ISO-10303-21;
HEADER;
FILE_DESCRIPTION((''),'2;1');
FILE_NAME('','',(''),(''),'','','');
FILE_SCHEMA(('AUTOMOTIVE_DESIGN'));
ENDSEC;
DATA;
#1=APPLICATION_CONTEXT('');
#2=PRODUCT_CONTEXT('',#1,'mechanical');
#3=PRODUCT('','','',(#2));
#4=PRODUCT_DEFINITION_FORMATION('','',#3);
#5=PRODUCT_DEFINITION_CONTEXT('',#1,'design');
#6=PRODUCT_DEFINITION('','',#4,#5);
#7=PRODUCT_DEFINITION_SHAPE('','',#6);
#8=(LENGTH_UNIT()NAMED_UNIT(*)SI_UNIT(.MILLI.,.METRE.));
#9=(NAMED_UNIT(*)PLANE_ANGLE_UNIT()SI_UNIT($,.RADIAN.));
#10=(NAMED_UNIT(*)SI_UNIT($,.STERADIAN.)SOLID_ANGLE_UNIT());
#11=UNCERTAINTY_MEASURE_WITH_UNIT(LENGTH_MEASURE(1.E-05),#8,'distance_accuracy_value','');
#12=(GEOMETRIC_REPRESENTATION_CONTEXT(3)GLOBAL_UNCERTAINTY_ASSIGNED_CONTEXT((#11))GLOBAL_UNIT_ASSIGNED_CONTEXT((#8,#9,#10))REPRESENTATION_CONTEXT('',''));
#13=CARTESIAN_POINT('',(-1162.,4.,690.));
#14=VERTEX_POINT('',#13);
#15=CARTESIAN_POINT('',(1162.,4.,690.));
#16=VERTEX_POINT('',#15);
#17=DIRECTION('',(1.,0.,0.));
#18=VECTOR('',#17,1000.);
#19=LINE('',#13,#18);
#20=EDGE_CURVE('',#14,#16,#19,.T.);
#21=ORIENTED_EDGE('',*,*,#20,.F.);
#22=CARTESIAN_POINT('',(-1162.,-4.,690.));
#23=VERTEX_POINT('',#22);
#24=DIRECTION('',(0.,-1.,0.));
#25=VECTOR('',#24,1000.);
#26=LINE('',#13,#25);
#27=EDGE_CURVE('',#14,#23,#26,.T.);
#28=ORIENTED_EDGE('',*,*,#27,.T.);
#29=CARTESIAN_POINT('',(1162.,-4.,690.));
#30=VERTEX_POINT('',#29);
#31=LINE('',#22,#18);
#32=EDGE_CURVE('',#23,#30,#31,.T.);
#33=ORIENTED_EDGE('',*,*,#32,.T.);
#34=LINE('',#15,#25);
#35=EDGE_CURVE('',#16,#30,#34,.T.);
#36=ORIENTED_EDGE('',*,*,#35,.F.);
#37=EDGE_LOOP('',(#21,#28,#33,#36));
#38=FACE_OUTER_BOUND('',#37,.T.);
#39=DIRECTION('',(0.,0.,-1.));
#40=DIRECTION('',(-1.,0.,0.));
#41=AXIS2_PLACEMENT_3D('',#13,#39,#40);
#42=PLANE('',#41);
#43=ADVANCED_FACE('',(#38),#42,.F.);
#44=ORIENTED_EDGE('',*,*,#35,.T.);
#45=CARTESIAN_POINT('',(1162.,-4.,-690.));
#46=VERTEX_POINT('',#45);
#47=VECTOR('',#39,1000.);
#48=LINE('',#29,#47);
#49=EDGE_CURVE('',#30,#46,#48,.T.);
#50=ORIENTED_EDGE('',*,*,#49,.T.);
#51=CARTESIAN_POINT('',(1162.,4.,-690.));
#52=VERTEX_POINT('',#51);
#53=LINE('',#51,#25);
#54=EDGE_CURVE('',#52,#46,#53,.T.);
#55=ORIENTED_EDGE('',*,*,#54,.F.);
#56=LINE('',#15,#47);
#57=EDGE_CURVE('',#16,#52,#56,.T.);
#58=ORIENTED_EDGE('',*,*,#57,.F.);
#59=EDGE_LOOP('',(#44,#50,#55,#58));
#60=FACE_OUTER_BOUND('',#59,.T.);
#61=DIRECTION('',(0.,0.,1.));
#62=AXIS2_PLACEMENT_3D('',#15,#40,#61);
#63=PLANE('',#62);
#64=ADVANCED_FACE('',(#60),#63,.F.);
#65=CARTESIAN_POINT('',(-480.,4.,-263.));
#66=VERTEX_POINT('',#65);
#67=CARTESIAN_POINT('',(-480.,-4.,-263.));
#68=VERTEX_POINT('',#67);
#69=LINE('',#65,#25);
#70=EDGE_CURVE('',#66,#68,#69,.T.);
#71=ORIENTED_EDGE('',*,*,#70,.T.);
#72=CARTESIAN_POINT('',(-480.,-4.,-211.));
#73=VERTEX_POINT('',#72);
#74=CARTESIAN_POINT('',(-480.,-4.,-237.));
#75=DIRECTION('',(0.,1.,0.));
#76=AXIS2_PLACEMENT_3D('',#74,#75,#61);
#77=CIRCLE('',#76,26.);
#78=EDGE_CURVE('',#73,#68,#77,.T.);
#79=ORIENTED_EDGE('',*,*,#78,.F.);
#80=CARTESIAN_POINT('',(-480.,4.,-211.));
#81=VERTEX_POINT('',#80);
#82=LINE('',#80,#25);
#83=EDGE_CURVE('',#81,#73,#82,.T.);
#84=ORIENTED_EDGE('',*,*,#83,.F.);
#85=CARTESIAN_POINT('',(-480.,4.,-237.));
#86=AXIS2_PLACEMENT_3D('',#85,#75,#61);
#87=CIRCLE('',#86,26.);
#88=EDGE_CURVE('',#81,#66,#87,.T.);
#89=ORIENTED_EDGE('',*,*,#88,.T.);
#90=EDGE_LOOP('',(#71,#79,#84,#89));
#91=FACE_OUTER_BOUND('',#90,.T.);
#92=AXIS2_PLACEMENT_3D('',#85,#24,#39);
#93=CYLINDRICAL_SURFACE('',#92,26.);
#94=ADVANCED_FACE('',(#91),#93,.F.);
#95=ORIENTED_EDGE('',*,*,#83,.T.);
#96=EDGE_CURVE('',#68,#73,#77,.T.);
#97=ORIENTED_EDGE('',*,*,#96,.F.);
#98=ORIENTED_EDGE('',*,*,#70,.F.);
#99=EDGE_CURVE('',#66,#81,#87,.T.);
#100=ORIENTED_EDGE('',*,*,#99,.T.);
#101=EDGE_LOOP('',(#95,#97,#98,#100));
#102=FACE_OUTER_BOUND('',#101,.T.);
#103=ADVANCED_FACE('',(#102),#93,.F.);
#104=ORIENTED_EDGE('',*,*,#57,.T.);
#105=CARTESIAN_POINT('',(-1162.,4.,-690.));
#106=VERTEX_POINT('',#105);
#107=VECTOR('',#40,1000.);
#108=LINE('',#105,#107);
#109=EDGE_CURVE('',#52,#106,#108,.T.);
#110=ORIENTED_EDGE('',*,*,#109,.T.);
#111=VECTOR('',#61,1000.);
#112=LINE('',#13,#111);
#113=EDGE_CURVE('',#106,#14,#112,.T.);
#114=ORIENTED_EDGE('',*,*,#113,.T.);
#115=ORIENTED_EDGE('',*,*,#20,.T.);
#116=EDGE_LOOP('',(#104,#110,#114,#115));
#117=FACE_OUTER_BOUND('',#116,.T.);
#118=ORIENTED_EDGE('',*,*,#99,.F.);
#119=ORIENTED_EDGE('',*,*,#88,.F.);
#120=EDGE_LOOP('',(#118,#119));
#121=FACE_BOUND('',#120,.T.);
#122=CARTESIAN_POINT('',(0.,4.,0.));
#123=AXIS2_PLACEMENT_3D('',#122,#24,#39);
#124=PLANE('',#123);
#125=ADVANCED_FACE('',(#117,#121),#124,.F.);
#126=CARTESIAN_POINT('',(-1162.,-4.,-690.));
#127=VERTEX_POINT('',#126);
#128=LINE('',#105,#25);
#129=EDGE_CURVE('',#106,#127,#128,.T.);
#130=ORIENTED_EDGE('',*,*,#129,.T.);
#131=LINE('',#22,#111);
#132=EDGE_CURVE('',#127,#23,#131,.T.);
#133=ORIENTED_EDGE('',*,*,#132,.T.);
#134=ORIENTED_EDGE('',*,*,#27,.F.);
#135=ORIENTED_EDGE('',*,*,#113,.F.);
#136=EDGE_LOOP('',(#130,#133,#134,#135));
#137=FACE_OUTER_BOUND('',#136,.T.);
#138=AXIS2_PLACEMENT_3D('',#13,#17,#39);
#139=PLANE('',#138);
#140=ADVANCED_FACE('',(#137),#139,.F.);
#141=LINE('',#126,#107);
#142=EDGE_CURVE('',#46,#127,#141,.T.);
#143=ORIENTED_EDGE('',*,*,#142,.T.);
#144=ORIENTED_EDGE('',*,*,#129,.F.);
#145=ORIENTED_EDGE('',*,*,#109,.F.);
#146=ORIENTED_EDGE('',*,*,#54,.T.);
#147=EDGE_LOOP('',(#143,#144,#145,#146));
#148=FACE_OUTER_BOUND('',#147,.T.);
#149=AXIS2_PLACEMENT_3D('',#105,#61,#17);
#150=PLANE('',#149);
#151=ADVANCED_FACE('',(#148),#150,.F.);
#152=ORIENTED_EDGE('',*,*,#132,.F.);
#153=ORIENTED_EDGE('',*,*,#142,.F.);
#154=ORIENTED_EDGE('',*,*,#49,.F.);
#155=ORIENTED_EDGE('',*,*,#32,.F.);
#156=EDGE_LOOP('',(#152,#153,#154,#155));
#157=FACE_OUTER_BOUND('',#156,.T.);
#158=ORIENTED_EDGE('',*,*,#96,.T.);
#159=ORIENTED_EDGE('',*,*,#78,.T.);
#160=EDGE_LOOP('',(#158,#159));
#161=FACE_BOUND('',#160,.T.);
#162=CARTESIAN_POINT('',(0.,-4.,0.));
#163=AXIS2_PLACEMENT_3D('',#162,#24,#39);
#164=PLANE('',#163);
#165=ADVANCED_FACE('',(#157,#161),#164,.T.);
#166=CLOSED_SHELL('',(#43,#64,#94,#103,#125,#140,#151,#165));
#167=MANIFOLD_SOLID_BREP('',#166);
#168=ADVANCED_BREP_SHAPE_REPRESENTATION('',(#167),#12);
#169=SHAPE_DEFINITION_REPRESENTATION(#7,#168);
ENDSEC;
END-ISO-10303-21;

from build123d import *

# Parameters (mm, degrees)
SKETCH_1_W      = 2324
SKETCH_1_H      = 1380
SKETCH_1_R      = 26
EXTRUDE_1_DEPTH = 4


with BuildPart() as part:
    # 草图1 → 凸台-拉伸1 (new, symmetric)
    with BuildSketch(Plane(origin=(0, 0, 0), x_dir=(1, 0, 0), z_dir=(0, 1, 0))):
        Rectangle(SKETCH_1_W, SKETCH_1_H)
        with Locations(Location((-480, 237, 0), (0, 0, 270))):
            Circle(SKETCH_1_R, mode=Mode.SUBTRACT)
    extrude(amount=EXTRUDE_1_DEPTH, both=True)


solid = part.part
